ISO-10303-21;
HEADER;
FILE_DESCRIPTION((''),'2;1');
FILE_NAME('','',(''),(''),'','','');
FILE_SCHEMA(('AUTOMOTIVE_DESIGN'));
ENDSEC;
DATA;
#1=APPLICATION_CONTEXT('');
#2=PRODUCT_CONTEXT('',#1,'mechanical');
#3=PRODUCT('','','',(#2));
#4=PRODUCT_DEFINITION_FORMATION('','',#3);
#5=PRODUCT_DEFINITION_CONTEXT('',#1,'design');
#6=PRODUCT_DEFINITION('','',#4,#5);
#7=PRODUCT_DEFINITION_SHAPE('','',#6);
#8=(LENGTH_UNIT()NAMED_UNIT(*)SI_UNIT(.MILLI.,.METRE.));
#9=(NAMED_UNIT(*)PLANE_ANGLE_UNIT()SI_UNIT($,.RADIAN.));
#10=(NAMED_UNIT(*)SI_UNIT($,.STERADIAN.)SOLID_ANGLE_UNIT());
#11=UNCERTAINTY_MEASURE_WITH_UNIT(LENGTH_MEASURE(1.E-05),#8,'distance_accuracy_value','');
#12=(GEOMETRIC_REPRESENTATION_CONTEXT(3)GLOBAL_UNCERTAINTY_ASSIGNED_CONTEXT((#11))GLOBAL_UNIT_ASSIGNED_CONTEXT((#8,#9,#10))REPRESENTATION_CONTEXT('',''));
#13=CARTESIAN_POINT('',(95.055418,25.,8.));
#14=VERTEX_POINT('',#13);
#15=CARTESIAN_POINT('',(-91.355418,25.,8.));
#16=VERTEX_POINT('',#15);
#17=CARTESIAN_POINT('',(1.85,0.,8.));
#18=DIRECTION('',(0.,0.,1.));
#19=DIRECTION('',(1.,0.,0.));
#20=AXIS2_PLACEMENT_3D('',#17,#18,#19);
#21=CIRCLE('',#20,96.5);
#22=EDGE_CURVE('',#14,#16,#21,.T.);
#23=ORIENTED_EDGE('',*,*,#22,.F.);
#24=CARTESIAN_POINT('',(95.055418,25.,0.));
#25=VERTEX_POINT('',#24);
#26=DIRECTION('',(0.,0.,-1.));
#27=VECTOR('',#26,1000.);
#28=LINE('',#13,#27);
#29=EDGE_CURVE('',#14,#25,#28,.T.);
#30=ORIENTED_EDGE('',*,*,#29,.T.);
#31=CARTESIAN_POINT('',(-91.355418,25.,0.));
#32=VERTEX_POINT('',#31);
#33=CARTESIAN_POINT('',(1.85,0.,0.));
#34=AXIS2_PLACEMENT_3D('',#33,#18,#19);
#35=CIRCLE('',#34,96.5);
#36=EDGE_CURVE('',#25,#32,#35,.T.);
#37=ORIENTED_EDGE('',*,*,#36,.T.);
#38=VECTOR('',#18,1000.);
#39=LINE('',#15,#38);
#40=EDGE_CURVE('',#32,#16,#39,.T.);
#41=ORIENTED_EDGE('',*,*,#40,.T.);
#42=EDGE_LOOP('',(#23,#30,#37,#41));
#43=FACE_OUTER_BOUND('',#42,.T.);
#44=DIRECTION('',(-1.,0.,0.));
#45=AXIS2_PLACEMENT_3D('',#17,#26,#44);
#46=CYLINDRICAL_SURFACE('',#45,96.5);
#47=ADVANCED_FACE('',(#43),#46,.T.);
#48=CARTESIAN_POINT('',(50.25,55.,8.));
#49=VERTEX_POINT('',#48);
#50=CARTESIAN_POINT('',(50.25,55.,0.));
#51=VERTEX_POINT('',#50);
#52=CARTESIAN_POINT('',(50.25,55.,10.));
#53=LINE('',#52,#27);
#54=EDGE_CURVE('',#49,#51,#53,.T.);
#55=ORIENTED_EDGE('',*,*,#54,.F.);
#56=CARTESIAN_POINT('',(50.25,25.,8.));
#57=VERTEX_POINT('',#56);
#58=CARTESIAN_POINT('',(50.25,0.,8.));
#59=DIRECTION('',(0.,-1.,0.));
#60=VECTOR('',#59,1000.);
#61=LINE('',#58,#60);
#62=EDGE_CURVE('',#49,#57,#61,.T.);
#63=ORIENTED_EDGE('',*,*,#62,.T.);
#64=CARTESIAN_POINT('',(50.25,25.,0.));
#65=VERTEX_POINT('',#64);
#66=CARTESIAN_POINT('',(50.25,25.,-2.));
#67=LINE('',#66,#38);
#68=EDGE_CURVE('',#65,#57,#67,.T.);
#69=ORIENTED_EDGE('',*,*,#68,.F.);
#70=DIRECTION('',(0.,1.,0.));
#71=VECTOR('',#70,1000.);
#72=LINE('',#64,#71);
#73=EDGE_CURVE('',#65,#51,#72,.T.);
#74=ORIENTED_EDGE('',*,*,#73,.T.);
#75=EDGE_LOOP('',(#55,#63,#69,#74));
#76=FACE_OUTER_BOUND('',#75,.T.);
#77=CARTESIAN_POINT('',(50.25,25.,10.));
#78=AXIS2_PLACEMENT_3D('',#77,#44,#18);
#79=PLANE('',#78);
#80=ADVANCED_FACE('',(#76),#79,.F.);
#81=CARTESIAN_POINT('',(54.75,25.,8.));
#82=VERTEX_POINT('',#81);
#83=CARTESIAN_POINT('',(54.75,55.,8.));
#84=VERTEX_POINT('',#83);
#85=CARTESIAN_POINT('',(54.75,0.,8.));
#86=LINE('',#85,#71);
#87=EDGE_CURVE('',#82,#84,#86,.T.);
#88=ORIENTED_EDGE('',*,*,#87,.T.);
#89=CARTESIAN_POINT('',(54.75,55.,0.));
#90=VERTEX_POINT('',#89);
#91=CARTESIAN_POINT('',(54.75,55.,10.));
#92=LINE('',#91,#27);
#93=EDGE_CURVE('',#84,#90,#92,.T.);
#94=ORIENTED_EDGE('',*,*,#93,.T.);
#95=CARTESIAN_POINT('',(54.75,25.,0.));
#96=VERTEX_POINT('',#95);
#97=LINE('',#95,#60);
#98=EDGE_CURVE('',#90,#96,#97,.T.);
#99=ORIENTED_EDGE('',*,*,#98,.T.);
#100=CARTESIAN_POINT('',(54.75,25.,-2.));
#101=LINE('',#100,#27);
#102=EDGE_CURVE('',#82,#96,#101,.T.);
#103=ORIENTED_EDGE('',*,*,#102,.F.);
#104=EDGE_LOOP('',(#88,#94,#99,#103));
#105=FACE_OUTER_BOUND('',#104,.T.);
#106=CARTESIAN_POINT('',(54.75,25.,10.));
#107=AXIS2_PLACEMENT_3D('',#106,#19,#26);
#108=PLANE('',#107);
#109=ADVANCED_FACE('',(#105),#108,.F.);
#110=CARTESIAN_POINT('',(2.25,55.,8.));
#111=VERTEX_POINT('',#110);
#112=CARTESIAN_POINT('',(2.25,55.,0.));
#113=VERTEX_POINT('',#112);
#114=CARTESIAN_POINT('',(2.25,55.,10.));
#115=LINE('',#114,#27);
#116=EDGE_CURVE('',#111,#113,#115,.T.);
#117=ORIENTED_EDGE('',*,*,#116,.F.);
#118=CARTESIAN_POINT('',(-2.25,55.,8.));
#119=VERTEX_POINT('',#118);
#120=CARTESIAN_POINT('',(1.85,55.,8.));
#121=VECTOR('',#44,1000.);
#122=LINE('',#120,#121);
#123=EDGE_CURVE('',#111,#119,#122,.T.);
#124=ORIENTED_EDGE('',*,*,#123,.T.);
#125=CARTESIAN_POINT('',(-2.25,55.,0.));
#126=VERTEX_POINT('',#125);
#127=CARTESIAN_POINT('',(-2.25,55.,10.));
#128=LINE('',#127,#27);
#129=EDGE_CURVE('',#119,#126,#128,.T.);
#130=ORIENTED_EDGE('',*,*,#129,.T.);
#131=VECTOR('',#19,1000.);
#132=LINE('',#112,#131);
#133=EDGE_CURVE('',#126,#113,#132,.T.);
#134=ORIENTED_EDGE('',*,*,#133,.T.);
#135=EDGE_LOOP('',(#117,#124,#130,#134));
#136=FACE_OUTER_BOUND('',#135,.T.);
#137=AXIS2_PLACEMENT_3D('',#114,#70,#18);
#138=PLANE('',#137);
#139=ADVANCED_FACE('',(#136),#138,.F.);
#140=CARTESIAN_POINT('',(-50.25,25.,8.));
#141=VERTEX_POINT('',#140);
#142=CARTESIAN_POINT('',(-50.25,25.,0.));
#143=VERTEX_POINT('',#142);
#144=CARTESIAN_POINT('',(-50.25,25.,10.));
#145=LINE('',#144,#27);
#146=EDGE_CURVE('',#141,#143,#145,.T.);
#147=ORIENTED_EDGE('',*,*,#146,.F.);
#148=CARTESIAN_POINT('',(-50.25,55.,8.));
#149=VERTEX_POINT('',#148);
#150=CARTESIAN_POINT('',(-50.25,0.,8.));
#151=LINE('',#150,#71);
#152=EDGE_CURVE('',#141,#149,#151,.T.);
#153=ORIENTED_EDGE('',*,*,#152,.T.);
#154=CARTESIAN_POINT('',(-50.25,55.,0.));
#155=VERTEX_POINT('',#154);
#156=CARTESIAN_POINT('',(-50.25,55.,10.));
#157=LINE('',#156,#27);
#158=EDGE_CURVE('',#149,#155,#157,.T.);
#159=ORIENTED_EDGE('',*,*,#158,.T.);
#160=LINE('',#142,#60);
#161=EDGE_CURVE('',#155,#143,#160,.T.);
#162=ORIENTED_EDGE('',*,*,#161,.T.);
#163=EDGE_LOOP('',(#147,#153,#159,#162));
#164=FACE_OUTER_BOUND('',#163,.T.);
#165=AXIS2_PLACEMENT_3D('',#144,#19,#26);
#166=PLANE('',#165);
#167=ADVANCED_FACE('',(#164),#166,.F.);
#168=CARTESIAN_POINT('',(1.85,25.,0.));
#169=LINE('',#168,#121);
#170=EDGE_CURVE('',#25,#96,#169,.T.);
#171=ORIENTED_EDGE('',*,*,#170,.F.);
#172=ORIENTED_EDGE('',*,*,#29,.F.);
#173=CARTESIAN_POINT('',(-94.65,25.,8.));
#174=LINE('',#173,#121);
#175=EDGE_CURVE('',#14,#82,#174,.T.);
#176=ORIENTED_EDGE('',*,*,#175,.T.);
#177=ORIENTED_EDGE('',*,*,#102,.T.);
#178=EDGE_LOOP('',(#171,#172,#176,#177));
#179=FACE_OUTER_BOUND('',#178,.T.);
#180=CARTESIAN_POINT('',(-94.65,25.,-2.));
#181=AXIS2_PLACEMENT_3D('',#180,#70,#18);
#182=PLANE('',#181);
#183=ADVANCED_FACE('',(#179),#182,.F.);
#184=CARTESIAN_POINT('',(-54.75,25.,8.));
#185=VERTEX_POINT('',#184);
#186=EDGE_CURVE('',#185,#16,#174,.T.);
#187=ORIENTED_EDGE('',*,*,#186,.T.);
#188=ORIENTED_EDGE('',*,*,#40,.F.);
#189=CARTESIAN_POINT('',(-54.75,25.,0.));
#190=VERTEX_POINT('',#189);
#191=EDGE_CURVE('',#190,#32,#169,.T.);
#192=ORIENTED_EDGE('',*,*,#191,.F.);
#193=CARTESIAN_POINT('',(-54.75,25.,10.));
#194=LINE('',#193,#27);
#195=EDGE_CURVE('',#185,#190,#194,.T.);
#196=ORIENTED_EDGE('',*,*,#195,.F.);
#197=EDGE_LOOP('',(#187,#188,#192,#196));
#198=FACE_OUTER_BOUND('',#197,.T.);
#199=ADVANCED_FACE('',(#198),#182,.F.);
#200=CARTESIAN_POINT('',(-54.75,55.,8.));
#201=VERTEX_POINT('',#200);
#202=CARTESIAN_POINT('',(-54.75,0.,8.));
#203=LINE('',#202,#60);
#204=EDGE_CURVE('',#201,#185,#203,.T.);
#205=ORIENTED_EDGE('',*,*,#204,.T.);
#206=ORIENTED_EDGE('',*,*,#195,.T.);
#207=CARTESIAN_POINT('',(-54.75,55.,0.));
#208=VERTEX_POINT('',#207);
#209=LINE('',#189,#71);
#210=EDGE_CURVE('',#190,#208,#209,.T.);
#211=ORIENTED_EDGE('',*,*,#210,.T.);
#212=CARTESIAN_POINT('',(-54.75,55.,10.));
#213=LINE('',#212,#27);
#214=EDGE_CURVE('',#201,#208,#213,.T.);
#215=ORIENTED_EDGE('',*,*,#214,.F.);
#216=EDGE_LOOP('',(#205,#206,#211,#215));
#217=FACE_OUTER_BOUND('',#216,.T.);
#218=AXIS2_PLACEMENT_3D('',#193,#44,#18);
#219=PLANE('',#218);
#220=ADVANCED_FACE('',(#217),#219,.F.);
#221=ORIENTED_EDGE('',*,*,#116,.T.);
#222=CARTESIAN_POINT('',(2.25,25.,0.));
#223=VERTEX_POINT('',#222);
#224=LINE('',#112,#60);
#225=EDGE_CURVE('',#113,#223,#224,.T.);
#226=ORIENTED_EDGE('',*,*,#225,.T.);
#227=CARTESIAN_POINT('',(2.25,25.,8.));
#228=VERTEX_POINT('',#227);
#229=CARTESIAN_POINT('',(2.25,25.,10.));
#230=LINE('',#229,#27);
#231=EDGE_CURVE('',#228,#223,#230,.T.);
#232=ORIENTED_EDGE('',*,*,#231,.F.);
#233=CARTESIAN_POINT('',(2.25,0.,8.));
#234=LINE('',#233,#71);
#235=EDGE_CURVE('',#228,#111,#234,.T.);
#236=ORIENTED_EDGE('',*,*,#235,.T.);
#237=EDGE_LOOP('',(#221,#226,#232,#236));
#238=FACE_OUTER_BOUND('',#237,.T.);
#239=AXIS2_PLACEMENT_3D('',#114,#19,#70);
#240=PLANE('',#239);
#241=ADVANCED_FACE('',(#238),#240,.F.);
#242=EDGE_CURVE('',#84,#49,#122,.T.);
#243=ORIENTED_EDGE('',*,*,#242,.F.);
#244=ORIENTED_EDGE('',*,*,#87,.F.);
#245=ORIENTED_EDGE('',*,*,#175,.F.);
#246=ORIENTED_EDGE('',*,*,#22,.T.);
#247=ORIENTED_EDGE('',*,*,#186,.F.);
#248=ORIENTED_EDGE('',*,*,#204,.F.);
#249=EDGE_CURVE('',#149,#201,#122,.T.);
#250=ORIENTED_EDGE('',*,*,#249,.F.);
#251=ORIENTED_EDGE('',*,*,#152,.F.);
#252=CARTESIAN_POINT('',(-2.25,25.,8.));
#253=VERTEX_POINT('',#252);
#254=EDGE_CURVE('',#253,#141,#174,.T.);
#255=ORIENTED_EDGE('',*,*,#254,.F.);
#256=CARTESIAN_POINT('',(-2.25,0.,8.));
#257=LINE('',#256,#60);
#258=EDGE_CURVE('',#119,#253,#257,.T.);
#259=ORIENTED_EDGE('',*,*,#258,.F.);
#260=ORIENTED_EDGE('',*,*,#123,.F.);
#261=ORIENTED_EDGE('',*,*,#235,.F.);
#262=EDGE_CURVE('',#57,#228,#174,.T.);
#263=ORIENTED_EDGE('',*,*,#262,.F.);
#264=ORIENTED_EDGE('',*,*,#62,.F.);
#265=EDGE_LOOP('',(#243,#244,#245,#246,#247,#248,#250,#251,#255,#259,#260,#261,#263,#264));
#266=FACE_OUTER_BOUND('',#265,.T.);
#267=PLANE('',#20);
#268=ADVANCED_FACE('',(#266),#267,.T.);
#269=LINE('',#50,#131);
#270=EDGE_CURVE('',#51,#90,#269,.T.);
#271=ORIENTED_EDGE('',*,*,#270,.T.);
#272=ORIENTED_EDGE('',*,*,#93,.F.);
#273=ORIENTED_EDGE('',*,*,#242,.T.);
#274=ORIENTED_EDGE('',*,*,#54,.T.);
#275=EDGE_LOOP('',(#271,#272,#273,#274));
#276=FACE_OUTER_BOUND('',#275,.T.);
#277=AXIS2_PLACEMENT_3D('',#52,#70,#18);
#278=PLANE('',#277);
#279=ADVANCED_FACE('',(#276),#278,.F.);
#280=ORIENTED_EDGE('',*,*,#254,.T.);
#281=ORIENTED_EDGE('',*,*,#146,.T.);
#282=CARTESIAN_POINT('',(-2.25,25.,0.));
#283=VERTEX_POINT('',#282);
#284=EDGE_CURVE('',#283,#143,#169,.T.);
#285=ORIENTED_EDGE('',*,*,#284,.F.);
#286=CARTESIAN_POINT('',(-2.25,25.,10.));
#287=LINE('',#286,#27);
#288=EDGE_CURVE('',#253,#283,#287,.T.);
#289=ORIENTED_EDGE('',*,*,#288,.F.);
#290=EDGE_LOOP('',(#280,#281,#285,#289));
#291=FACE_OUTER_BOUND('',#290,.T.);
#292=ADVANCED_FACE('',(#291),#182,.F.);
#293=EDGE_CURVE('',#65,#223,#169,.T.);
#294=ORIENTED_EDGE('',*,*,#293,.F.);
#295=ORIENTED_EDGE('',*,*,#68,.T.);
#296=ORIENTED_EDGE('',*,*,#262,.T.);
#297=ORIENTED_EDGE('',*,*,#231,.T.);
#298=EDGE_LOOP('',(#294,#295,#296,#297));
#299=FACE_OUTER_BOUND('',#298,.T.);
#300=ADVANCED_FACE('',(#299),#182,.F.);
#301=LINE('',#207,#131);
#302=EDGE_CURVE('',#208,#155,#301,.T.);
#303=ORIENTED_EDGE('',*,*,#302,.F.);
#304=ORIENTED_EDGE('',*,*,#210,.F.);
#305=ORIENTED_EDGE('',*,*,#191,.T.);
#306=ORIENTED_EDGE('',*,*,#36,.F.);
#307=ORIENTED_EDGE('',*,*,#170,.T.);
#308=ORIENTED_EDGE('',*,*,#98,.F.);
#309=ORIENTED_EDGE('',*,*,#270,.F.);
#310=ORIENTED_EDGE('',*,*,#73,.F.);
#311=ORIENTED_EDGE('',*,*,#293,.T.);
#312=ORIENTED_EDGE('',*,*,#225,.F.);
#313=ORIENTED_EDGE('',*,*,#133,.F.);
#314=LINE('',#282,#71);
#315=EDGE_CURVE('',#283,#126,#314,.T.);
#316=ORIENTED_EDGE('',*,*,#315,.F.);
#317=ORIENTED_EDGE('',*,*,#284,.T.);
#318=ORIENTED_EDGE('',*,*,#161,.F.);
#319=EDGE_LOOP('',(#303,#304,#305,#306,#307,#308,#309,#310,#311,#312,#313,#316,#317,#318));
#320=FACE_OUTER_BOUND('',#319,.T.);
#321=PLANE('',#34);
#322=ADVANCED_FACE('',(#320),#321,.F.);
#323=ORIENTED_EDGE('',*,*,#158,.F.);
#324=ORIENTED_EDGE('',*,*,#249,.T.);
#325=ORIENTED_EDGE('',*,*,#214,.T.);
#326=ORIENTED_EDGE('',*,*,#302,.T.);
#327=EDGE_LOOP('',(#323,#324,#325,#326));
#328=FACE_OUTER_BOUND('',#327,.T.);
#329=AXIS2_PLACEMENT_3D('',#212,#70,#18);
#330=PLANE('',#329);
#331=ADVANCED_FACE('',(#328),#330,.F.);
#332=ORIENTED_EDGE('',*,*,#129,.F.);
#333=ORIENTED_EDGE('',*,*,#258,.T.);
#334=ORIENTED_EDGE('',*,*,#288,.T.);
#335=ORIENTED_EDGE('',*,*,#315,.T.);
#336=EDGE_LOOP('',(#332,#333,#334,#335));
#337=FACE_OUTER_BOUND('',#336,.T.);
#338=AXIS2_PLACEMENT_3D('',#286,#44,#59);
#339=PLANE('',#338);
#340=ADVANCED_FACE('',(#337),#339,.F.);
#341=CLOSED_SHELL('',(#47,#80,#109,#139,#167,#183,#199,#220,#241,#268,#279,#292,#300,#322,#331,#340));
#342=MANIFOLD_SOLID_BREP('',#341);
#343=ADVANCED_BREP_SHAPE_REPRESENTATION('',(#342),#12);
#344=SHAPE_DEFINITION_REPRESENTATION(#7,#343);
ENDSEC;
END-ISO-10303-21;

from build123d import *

# Parameters (mm, degrees)
BOSS_EXTRUDE1_DEPTH = 8
CUT_EXTRUDE1_DEPTH  = 10
SKETCH3_W           = 4.5
SKETCH3_H           = 30
CUT_EXTRUDE2_DEPTH  = 10


with BuildPart() as part:
    # Sketch1 → Boss-Extrude1 (new body)
    with BuildSketch(Plane.XY):
        with BuildLine():
            Line((-94.65, 0), (98.35, 0))
            ThreePointArc((98.35, 0), (1.85, 96.5), (-94.65, 0))
        make_face()
    extrude(amount=BOSS_EXTRUDE1_DEPTH)

    # Sketch2 → Cut-Extrude1 (cut)
    with BuildSketch(Plane.XY.offset(8)):
        Polygon((-94.65, 0), (-94.65, 25), (109.452328138, 25), (98.649241205, -24.174377991), align=None)
    extrude(amount=-CUT_EXTRUDE1_DEPTH, mode=Mode.SUBTRACT)

    # Sketch3 → Cut-Extrude2 (cut)
    with BuildSketch(Plane(origin=(0, 0, 0), x_dir=(-1, 0, 0), z_dir=(0, 0, -1))):
        with Locations((0, 40)):
            Rectangle(SKETCH3_W, SKETCH3_H)
        with Locations((52.5, 40)):
            Rectangle(SKETCH3_W, SKETCH3_H)
        with Locations((-52.5, 40)):
            Rectangle(SKETCH3_W, SKETCH3_H)
    extrude(amount=-CUT_EXTRUDE2_DEPTH, mode=Mode.SUBTRACT)


solid = part.part
